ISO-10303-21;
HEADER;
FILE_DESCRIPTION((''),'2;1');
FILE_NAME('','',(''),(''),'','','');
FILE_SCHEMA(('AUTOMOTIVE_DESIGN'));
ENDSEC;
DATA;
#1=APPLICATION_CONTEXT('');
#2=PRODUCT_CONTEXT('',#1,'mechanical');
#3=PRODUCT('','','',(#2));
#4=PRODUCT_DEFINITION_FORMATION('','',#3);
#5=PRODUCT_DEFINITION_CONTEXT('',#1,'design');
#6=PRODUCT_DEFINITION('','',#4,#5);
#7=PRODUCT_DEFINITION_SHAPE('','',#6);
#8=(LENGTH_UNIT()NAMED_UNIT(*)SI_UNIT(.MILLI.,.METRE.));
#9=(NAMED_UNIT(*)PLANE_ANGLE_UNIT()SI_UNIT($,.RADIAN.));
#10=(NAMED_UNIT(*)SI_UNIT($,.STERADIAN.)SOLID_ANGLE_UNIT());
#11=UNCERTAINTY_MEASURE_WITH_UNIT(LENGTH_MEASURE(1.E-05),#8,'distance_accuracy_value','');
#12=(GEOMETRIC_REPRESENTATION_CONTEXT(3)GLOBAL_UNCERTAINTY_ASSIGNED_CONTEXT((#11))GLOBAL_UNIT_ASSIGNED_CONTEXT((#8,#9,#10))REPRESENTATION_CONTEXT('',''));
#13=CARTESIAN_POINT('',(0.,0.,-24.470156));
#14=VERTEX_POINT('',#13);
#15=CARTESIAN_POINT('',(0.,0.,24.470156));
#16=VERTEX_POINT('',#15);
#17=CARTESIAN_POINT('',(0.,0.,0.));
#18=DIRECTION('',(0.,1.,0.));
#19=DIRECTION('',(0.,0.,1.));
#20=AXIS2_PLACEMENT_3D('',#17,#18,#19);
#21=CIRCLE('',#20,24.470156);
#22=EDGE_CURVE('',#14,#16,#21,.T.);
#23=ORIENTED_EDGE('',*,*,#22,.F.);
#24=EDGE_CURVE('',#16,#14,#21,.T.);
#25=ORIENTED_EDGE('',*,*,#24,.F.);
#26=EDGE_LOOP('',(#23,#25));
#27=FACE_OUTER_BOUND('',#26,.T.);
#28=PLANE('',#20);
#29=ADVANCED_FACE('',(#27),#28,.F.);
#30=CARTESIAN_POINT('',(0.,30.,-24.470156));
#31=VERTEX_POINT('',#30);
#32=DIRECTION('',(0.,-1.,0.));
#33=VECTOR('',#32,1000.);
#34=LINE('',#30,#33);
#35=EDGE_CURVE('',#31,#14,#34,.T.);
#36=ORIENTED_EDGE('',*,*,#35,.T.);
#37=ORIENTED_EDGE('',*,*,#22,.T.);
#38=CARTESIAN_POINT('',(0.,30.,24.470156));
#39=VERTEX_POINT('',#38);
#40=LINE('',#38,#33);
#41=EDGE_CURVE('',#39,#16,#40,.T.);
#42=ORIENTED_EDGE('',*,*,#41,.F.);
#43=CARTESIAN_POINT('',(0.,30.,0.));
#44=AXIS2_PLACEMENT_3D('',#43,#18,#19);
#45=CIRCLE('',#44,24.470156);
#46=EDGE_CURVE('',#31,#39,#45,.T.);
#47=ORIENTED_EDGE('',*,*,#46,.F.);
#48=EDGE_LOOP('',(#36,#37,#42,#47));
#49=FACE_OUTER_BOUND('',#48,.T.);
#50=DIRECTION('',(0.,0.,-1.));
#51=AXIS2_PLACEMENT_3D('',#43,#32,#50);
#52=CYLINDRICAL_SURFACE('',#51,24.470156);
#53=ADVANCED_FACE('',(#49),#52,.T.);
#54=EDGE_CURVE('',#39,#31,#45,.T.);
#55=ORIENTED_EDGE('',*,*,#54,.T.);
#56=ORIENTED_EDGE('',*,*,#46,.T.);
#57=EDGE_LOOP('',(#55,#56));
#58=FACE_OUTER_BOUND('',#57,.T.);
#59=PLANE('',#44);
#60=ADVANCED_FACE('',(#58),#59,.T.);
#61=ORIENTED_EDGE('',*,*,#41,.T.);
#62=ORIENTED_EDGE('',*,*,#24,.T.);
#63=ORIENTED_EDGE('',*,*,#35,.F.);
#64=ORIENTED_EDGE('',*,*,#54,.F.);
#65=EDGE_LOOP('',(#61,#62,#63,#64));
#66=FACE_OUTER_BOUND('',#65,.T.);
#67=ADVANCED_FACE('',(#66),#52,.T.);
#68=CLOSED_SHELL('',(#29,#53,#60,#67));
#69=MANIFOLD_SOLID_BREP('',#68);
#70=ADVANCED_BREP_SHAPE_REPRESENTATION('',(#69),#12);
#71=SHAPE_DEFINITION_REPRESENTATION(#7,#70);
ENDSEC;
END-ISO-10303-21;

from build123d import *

# Parameters (mm, degrees)
SKETCH_1_R      = 24.470155971
EXTRUDE_1_DEPTH = 30


with BuildPart() as part:
    # 草图1 → 凸台-拉伸1 (new body)
    with BuildSketch(Plane(origin=(0, 0, 0), x_dir=(1, 0, 0), z_dir=(0, 1, 0))):
        with Locations(Location((0, 0, 0), (0, 0, 270))):
            Circle(SKETCH_1_R)
    extrude(amount=EXTRUDE_1_DEPTH)


solid = part.part
